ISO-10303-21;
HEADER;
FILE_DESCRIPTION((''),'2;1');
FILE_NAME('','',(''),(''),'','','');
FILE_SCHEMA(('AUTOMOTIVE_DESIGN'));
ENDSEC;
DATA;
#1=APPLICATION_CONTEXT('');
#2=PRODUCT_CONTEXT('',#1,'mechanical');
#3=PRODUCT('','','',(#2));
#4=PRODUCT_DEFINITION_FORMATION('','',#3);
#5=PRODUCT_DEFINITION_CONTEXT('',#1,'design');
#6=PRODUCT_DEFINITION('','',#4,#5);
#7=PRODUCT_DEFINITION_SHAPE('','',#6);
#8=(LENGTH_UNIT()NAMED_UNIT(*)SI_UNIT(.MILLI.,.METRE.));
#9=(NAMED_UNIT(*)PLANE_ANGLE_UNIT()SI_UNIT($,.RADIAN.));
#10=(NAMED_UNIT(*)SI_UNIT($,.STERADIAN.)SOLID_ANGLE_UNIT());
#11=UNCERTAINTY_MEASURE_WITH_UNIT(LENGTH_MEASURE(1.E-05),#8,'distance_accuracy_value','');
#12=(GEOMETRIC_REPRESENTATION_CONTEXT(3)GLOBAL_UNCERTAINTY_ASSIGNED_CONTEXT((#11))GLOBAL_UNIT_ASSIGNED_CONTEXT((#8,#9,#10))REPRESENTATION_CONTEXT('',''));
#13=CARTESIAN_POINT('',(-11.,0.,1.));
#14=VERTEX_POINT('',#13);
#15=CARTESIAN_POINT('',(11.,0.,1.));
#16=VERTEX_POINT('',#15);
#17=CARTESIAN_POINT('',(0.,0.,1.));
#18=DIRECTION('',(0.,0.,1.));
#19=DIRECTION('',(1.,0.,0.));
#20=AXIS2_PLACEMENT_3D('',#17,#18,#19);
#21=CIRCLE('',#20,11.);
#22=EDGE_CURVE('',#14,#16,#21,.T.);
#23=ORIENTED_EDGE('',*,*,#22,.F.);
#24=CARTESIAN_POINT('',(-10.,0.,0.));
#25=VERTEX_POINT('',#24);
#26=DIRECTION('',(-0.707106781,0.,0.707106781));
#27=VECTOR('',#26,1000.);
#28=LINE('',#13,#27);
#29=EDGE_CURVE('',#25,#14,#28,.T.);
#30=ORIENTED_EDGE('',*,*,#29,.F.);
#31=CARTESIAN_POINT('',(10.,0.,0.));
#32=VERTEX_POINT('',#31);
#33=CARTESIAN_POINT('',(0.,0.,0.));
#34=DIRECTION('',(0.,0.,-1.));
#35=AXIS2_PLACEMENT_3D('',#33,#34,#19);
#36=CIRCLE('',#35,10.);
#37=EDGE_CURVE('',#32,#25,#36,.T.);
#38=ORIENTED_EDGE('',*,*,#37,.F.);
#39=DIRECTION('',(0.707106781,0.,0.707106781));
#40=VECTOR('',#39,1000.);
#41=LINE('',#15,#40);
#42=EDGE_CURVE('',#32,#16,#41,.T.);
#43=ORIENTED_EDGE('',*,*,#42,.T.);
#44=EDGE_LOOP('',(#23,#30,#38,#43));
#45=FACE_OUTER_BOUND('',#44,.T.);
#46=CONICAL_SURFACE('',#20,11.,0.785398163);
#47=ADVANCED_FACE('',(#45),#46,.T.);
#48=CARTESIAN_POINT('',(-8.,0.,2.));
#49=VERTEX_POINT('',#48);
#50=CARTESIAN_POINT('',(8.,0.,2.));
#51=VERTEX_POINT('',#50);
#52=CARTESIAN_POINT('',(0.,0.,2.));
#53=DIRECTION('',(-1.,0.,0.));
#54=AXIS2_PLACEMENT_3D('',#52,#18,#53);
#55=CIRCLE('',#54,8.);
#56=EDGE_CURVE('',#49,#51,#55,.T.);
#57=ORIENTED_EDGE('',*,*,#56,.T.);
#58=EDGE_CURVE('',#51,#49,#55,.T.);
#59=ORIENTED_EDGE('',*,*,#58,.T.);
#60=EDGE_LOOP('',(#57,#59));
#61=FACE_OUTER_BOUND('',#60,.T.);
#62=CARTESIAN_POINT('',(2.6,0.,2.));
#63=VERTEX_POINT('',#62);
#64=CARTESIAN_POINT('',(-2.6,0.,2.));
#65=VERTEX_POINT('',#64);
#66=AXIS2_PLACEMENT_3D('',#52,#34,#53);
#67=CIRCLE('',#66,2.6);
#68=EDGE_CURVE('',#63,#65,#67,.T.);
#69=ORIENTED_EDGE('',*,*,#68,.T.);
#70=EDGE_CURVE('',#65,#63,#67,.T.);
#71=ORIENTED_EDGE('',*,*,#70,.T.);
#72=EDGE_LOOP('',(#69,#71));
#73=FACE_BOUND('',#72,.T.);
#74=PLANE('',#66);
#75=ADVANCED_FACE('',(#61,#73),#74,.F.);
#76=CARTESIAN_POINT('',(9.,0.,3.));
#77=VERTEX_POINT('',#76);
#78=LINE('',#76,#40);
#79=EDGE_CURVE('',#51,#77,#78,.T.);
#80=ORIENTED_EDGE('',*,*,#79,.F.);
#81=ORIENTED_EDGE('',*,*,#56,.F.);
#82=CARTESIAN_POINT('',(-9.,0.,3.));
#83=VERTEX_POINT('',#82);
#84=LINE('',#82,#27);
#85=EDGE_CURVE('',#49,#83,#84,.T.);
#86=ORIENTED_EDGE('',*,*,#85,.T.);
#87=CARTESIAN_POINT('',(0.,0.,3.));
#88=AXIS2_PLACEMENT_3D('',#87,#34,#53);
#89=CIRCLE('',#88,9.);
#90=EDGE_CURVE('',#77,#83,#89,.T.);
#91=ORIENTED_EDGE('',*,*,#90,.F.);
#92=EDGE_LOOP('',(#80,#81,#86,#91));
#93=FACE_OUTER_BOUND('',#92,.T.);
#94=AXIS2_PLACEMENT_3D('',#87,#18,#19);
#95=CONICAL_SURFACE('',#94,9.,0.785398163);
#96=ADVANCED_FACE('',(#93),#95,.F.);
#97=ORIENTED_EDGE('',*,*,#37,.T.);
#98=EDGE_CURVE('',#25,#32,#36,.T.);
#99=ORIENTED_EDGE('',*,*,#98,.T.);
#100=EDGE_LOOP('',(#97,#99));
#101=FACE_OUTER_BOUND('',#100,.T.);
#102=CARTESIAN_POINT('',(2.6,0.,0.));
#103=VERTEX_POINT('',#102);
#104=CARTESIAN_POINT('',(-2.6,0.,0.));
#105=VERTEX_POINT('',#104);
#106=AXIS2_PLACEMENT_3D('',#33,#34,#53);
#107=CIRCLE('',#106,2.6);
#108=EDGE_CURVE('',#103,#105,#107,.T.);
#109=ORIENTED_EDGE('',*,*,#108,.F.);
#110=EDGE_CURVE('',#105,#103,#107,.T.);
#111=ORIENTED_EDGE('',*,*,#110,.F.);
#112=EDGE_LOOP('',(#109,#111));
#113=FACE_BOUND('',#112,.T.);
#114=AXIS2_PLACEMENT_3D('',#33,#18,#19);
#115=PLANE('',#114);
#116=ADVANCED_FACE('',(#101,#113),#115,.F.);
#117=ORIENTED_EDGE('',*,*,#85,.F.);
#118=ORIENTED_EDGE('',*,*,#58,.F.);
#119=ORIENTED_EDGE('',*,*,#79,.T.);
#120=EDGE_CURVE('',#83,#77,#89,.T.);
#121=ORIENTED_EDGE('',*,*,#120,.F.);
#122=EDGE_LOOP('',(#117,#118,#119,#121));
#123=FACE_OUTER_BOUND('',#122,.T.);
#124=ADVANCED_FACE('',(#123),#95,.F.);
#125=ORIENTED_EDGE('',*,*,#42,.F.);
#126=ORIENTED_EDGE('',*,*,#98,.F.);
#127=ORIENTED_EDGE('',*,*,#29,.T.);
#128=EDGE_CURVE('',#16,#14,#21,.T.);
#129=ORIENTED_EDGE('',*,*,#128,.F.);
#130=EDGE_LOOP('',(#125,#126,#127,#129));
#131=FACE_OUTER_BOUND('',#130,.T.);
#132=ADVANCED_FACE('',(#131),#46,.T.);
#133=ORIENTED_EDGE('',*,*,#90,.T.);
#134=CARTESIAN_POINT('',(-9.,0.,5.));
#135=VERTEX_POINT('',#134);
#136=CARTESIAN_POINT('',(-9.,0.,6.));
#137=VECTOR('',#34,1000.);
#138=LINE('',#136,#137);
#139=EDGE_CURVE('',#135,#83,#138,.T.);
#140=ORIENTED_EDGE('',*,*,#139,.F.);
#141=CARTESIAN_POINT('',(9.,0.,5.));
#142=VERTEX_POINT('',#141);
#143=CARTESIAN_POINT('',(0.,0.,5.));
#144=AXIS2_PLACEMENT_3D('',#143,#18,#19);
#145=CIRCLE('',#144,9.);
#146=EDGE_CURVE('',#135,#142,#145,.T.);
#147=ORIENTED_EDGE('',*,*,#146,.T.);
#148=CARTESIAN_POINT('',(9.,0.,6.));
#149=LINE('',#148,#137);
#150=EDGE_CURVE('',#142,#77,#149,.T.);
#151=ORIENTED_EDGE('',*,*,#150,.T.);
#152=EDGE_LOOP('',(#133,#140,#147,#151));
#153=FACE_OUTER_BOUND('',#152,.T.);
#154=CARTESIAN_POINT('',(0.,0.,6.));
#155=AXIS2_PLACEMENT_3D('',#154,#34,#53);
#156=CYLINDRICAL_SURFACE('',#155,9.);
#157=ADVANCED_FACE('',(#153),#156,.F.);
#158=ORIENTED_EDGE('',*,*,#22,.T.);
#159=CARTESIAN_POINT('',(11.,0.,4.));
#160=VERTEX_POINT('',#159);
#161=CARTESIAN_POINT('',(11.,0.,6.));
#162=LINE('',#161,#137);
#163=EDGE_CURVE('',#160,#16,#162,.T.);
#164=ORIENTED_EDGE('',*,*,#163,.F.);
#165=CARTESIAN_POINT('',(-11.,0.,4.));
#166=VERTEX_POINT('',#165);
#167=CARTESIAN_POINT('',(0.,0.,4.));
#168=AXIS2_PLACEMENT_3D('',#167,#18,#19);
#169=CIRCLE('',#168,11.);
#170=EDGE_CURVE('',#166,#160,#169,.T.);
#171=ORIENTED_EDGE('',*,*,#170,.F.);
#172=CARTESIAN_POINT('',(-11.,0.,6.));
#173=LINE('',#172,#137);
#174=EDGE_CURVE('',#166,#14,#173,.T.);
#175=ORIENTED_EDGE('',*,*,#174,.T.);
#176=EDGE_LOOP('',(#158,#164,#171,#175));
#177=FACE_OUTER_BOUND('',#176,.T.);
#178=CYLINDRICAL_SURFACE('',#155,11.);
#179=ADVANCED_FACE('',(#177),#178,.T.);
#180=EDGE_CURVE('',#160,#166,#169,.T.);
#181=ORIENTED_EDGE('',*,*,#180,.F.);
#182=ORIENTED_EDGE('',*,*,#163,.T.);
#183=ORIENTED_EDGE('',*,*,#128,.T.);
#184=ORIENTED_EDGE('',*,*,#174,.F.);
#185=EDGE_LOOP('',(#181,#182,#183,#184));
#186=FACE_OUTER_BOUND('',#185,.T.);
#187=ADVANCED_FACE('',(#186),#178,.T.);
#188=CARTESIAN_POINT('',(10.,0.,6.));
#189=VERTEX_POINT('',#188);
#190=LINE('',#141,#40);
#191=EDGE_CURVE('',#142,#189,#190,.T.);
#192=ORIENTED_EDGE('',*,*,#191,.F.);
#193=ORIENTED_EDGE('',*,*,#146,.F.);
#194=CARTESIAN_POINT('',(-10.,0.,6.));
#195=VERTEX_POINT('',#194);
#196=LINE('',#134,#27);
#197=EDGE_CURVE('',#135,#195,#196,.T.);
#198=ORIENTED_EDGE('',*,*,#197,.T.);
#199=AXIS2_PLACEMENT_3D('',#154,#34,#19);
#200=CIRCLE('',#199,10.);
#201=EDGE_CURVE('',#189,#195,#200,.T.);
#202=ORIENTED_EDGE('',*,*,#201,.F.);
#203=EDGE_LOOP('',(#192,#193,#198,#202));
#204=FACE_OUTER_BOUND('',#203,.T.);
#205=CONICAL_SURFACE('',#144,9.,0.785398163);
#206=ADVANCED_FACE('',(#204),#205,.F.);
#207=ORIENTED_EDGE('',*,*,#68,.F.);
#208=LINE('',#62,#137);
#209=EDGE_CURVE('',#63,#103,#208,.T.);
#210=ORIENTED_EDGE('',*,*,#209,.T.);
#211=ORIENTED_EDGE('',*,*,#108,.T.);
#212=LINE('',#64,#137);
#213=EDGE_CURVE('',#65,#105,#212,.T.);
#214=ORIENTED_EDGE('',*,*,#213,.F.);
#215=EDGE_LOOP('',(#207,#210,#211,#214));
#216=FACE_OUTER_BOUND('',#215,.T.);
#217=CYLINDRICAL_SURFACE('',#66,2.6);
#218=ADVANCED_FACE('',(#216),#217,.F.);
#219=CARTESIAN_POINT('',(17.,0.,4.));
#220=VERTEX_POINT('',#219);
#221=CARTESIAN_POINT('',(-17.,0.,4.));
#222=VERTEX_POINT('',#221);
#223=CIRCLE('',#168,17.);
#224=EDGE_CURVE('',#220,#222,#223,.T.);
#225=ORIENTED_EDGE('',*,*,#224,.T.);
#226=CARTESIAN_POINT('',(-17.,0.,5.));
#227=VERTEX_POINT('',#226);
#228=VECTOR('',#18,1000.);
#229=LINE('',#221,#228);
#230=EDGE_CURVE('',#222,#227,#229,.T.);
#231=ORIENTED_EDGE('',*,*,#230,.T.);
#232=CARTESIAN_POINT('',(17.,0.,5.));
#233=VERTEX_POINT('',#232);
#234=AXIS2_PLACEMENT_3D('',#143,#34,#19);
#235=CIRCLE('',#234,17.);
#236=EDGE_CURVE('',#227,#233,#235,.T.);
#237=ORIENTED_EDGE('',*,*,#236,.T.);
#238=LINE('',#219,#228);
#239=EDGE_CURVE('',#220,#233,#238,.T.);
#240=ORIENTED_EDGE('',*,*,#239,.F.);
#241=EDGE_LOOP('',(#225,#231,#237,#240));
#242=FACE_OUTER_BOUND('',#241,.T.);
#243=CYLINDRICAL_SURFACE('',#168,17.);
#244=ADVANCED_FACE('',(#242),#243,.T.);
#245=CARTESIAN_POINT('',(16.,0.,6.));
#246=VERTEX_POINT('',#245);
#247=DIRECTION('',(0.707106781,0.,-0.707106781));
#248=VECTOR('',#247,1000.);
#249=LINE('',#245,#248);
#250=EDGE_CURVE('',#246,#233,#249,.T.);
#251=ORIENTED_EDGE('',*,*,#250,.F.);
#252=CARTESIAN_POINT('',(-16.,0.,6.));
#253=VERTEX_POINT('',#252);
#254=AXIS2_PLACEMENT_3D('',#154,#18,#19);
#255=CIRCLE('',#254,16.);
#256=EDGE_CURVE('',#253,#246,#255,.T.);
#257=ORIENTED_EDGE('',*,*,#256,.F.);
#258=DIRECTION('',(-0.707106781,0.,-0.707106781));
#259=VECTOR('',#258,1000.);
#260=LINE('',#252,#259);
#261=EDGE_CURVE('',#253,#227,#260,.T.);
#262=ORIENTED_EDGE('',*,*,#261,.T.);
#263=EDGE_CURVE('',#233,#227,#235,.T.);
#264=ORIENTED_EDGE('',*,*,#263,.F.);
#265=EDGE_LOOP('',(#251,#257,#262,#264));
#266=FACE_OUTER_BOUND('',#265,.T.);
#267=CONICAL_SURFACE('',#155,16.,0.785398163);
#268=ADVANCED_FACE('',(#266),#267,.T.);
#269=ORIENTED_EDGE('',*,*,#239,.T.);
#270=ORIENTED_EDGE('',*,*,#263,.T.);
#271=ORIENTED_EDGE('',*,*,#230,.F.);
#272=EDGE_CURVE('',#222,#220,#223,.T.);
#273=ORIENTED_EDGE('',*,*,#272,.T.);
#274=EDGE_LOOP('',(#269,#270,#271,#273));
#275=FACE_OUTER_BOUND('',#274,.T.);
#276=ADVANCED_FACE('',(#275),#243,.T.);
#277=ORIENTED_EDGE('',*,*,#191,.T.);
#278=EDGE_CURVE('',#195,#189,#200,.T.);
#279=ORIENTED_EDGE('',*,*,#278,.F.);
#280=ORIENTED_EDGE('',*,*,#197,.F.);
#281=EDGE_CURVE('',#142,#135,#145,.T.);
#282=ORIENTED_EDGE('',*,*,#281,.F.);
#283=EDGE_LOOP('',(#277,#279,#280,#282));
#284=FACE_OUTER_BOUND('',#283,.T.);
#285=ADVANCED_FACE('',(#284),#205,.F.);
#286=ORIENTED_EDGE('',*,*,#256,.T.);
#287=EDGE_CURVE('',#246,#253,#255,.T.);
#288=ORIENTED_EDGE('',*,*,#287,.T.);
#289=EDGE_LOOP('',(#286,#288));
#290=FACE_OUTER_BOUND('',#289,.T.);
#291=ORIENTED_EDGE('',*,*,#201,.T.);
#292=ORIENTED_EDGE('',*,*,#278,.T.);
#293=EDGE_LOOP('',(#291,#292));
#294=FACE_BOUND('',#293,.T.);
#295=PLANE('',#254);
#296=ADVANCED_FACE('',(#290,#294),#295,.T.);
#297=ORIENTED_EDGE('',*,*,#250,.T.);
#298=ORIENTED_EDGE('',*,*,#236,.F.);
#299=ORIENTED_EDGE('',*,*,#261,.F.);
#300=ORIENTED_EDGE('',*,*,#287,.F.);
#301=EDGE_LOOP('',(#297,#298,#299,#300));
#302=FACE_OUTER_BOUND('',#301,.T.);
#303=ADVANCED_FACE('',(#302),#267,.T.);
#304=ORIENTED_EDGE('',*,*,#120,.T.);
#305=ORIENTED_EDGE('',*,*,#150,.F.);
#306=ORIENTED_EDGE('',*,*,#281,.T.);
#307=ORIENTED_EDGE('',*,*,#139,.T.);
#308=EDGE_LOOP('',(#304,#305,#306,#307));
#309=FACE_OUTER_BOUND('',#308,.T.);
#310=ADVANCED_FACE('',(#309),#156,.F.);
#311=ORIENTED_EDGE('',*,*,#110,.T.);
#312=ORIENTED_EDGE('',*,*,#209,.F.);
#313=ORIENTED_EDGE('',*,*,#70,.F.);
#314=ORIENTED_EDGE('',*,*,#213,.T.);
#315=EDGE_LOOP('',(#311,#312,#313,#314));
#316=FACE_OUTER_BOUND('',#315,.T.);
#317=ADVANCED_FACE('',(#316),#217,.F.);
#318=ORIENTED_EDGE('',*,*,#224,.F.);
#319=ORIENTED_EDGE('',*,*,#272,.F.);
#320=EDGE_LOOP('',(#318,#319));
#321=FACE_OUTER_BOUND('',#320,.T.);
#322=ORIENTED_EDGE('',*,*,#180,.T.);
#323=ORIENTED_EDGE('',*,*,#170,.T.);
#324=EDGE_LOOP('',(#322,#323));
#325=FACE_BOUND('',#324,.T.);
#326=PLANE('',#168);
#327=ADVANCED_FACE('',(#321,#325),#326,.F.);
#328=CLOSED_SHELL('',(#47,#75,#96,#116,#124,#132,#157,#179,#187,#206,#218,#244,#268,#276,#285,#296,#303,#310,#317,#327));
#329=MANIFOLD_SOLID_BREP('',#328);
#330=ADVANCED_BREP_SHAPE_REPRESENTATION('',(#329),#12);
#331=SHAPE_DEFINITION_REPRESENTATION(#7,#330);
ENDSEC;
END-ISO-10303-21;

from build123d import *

# Parameters (mm, degrees)
SKETCH_1_R      = 11
SKETCH_1_R_2    = 9
EXTRUDE_1_DEPTH = 6
SKETCH_2_R      = 11
SKETCH_2_R_2    = 2.6
EXTRUDE_2_DEPTH = 2
CHAMFER_1_SIZE  = 1
EXTRUDE_START   = -2
SKETCH_3_R      = 17
SKETCH_3_R_2    = 9
EXTRUDE_3_DEPTH = 2
CHAMFER_2_SIZE  = 1


with BuildPart() as part:
    # 草图1 → 凸台-拉伸1 (new body)
    with BuildSketch(Plane.XY):
        Circle(SKETCH_1_R)
        Circle(SKETCH_1_R_2, mode=Mode.SUBTRACT)
    extrude(amount=EXTRUDE_1_DEPTH)

    # 草图2 → 凸台-拉伸2 (add)
    with BuildSketch(Plane(origin=(0, 0, 0), x_dir=(-1, 0, 0), z_dir=(0, 0, -1))):
        with Locations(Location((0, 0, 0), (0, 0, 180))):
            Circle(SKETCH_2_R)
        Circle(SKETCH_2_R_2, mode=Mode.SUBTRACT)
    extrude(amount=-EXTRUDE_2_DEPTH)

    # 倒角1
    chamfer_1_edges = [part.edges().sort_by_distance(p)[0] for p in [
        (-9, 0, 2),
        (-11, 0, 0),
    ]]
    chamfer(chamfer_1_edges, length=CHAMFER_1_SIZE)

    # 草图3 → 凸台-拉伸3 (add)
    with BuildSketch(Plane.XY.offset(6).offset(EXTRUDE_START)):
        Circle(SKETCH_3_R)
        with Locations(Location((0, 0, 0), (0, 0, 180))):
            Circle(SKETCH_3_R_2, mode=Mode.SUBTRACT)
    extrude(amount=EXTRUDE_3_DEPTH)

    # 倒角2
    chamfer_2_edges = [part.edges().sort_by_distance(p)[0] for p in [
        (-17, 0, 6),
        (-9, 0, 6),
    ]]
    chamfer(chamfer_2_edges, length=CHAMFER_2_SIZE)


solid = part.part
